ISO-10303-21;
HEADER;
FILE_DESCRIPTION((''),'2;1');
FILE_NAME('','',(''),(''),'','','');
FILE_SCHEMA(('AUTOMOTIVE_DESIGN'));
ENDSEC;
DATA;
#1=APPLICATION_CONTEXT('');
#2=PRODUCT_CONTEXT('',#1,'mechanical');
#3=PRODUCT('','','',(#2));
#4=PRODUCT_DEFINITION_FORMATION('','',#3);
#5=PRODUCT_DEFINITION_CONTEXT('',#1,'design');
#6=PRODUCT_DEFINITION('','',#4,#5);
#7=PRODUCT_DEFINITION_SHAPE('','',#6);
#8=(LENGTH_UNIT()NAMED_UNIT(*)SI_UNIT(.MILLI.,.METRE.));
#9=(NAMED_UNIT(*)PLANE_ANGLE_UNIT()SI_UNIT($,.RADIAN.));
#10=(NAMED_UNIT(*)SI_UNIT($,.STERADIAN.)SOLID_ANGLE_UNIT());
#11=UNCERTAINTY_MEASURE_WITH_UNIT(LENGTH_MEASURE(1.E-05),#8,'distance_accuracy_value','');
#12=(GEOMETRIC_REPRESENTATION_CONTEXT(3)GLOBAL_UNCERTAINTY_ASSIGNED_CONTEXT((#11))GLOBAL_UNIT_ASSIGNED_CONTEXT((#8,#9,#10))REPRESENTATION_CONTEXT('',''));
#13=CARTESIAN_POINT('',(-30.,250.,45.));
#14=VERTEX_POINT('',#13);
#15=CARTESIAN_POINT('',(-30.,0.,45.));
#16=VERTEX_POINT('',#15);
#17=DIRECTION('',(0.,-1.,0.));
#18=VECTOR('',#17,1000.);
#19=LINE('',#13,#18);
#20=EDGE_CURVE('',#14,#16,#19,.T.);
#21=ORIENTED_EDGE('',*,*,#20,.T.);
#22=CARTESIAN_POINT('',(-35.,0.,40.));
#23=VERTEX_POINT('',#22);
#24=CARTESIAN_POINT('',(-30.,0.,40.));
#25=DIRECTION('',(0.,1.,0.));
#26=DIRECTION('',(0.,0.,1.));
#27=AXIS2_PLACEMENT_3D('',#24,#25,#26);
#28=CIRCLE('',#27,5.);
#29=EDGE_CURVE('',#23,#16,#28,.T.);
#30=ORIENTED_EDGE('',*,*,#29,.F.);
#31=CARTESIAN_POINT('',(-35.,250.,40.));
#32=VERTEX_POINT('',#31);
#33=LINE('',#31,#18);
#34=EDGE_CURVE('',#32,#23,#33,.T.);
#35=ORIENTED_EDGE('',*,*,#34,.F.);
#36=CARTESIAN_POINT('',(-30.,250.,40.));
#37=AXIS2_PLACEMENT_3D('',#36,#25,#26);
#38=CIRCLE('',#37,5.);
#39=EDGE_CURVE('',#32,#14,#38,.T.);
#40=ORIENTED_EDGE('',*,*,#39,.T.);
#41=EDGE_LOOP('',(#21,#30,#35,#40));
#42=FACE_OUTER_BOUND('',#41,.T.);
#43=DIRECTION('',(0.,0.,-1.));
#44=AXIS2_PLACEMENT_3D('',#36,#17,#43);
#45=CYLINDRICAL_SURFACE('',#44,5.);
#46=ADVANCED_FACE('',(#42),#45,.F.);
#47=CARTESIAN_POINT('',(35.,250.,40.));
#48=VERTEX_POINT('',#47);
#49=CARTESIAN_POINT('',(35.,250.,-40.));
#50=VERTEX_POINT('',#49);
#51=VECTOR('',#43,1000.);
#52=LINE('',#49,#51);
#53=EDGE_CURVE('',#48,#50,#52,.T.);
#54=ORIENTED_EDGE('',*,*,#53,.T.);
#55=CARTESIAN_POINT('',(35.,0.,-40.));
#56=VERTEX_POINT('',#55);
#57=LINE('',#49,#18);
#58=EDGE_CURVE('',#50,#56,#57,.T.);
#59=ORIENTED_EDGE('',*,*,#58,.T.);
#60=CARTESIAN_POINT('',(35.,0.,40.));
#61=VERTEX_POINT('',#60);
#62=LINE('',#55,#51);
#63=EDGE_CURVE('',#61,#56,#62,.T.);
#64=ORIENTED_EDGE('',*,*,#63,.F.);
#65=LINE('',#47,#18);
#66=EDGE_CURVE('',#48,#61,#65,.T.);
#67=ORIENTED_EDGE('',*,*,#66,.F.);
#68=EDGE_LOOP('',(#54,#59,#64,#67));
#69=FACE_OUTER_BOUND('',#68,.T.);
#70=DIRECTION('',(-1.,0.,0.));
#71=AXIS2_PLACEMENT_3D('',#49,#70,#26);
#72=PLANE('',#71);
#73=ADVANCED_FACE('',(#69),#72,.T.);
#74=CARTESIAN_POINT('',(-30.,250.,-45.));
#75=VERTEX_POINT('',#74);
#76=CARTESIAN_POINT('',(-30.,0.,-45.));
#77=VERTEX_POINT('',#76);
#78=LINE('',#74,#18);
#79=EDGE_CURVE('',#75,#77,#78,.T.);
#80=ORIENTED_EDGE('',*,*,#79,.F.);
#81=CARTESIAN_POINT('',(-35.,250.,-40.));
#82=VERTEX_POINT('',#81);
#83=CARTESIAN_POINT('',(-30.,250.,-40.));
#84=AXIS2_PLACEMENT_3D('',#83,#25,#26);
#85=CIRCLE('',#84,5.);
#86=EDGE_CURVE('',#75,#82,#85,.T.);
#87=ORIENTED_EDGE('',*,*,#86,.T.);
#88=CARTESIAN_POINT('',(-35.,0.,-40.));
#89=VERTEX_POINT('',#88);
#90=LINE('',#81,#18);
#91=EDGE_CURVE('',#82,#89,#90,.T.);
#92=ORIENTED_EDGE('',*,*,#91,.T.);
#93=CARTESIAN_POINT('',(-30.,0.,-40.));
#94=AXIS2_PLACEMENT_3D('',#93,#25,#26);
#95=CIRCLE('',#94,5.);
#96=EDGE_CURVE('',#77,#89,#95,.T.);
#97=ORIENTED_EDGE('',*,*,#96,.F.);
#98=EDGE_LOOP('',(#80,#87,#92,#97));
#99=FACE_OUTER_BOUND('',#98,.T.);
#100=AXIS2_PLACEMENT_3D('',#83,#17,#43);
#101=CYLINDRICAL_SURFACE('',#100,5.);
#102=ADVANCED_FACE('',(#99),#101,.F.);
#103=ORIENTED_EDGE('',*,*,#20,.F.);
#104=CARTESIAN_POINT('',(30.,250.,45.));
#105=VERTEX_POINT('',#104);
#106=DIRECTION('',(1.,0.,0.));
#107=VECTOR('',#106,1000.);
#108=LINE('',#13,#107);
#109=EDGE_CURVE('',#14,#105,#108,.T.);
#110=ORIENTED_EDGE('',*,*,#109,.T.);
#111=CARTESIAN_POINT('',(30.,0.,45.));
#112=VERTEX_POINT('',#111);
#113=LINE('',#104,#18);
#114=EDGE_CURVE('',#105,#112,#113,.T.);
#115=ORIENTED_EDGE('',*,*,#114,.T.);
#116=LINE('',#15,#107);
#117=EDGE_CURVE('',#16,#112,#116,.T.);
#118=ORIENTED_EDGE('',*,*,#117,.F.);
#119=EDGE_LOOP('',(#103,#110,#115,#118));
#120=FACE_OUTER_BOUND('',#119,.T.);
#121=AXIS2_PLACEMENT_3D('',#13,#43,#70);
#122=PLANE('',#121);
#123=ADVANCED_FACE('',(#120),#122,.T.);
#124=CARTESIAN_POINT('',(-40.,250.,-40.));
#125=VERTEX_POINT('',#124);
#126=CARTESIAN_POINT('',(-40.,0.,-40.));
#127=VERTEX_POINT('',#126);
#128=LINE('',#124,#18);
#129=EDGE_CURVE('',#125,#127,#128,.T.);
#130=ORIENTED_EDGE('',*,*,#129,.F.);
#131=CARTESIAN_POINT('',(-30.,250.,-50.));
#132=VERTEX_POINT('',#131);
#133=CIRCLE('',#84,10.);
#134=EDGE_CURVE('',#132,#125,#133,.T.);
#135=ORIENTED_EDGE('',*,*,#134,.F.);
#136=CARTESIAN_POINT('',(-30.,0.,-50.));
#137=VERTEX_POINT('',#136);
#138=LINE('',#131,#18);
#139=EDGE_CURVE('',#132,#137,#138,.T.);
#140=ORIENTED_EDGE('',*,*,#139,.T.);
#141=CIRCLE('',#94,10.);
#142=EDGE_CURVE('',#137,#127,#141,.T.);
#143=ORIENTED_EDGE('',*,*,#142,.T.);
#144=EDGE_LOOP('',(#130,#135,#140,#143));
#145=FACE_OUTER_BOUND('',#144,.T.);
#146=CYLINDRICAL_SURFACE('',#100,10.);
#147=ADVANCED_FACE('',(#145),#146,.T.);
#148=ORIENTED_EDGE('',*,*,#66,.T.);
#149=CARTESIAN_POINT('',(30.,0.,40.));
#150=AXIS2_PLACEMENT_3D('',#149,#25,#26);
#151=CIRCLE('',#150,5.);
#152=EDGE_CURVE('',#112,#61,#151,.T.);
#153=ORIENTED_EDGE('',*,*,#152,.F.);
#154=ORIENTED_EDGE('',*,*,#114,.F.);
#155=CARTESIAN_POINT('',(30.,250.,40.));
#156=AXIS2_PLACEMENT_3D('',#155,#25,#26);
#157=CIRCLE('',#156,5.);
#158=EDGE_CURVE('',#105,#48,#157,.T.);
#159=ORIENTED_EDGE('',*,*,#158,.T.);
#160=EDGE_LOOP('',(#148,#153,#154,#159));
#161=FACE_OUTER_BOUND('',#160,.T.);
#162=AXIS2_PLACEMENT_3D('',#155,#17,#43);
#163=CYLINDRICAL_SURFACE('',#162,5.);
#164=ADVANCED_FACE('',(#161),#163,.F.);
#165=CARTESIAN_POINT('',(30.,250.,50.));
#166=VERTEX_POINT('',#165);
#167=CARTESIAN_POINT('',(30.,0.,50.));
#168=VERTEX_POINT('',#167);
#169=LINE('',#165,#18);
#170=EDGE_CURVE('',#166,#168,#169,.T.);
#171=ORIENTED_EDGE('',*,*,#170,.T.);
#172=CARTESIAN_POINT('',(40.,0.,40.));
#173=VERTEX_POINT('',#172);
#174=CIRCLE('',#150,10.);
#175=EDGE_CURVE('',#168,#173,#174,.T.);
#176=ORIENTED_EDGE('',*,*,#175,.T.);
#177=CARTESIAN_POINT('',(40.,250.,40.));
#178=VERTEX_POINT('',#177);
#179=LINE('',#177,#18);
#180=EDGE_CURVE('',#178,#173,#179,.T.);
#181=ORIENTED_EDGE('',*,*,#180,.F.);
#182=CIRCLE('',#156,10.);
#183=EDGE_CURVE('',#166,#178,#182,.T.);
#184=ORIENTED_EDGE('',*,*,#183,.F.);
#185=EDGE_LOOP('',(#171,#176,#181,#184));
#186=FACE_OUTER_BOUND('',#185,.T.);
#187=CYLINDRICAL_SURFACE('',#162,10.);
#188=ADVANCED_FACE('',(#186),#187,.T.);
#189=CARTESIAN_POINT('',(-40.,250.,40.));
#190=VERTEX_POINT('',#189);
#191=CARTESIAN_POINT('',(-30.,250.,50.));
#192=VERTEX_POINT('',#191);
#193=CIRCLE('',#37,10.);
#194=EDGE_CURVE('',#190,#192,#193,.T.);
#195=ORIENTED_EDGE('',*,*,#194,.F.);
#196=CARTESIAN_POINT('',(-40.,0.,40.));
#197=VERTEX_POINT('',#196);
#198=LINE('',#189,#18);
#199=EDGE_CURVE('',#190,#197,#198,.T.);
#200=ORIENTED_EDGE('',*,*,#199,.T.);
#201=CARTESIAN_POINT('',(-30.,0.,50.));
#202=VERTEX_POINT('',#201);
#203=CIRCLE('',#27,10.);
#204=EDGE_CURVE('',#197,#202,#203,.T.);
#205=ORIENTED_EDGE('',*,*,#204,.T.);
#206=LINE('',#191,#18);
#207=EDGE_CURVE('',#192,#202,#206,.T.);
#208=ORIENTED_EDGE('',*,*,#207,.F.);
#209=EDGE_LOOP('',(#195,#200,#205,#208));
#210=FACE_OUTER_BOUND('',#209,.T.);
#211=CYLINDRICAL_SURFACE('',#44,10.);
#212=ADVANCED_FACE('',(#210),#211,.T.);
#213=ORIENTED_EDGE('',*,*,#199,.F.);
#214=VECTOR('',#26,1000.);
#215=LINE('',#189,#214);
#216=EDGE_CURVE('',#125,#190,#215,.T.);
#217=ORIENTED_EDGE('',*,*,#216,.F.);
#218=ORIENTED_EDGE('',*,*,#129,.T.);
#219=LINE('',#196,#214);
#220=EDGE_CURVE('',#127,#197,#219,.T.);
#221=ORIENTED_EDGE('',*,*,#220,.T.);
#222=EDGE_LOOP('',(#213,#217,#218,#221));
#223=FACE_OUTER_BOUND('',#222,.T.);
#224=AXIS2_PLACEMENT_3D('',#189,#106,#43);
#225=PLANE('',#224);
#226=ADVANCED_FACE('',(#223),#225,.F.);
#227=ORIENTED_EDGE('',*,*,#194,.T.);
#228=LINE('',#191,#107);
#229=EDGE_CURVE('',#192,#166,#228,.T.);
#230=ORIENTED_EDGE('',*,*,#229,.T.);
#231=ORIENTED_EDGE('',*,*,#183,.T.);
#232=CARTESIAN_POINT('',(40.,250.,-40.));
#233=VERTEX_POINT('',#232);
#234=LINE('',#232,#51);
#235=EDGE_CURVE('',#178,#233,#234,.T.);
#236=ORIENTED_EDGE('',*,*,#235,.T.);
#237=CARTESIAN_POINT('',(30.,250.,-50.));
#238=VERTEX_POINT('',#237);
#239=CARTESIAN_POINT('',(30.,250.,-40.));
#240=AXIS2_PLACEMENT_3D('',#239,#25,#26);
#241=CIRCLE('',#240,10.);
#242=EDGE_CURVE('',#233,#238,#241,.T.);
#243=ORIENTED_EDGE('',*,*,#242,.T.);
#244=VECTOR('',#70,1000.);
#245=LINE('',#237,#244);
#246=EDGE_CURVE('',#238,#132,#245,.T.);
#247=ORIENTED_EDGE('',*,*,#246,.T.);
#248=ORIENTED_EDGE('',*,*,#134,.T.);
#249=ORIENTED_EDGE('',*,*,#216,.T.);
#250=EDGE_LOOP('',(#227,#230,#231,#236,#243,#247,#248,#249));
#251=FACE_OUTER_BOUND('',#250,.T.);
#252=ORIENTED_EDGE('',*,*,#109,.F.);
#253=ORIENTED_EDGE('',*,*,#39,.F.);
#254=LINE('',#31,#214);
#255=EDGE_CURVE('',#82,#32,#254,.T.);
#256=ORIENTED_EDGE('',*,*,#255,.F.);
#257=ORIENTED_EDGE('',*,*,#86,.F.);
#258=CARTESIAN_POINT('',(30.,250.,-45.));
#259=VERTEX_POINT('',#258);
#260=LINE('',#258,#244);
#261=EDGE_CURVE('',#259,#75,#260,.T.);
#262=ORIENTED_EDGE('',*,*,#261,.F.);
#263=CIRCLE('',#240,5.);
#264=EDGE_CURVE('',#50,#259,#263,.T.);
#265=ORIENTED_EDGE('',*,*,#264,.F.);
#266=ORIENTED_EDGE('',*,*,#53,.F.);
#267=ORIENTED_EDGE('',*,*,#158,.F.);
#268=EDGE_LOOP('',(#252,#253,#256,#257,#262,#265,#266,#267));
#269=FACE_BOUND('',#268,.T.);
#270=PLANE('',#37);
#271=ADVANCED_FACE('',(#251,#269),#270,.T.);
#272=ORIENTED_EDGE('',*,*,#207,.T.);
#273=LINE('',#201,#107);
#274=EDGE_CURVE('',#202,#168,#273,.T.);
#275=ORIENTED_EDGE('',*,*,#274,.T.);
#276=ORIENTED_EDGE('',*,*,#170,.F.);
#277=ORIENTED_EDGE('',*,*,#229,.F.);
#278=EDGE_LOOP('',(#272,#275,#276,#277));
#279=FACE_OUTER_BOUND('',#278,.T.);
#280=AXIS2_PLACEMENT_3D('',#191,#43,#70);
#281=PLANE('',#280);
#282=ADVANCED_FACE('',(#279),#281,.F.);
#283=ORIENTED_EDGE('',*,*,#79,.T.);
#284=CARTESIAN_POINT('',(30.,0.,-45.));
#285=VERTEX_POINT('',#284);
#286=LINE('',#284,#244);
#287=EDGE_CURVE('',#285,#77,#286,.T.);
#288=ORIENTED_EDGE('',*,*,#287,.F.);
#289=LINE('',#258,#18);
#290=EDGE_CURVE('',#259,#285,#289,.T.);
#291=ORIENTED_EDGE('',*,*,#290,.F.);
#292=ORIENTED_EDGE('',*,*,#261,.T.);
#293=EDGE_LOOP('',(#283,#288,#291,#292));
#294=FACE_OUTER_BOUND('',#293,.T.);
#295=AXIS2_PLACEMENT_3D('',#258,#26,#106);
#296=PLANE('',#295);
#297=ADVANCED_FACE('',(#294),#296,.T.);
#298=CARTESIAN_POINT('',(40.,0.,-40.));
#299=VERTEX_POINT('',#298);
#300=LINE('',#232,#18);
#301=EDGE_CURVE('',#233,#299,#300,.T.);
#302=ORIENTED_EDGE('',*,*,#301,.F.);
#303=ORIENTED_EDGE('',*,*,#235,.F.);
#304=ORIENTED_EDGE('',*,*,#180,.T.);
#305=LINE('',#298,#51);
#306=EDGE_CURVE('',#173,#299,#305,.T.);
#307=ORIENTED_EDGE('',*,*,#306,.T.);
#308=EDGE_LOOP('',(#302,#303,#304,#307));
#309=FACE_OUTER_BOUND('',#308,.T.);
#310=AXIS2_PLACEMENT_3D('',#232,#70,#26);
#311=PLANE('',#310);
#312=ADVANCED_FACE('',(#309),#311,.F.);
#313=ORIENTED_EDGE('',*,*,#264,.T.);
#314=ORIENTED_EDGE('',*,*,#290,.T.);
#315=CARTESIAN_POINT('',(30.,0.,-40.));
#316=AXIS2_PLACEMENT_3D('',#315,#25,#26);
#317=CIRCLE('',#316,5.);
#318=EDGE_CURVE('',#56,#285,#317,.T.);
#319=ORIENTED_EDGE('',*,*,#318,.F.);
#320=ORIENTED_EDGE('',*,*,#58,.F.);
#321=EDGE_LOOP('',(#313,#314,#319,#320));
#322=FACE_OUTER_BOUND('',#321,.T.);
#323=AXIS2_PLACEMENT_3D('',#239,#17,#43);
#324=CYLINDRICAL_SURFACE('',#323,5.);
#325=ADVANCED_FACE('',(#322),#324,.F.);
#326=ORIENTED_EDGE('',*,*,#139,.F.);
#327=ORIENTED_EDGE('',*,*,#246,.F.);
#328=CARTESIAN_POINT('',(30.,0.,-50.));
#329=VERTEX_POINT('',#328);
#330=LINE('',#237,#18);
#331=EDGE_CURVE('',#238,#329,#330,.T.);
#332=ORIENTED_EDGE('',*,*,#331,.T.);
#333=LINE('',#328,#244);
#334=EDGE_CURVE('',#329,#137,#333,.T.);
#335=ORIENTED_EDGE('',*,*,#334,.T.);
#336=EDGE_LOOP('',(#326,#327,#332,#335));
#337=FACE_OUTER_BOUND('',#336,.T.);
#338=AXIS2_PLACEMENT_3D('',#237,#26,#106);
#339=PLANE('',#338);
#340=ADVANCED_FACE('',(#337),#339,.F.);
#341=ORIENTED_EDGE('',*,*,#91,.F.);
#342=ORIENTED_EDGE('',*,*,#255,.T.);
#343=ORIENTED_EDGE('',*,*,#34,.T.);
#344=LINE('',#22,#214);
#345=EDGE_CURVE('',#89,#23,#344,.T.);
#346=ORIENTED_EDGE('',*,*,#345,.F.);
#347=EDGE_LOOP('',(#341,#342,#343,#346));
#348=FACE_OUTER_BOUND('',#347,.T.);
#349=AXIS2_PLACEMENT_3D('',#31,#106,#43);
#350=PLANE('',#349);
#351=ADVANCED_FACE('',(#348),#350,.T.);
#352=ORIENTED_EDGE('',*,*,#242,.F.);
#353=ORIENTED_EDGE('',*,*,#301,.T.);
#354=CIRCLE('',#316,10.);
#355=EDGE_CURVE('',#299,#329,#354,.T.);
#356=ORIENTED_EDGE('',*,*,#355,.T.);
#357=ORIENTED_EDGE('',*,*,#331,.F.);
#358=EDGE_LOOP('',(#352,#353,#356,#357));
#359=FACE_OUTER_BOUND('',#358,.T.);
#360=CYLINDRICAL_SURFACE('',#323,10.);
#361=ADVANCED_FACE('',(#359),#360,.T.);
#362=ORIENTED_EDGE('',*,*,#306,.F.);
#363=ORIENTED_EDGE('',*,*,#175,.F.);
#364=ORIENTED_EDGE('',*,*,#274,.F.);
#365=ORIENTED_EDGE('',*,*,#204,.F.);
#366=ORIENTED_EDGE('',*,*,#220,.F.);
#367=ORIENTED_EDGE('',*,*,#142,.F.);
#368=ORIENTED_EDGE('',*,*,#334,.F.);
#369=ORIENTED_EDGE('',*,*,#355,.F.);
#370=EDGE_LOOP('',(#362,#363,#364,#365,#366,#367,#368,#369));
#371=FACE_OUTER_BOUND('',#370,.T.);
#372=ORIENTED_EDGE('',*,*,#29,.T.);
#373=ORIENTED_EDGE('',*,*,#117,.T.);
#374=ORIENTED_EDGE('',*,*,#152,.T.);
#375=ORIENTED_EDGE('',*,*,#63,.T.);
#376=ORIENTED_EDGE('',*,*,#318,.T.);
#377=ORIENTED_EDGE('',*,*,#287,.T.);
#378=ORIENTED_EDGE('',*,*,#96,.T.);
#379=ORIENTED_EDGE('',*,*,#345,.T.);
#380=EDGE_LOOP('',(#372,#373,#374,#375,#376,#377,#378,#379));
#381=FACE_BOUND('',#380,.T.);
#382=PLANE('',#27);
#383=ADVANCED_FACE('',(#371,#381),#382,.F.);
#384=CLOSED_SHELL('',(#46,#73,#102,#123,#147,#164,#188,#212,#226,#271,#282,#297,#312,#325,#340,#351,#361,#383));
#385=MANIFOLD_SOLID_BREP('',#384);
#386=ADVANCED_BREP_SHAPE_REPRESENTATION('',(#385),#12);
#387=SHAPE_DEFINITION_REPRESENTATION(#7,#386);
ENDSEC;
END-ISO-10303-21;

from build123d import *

# Parameters (mm, degrees)
GB_T_6728_2002_RECTANGULAR_HOLLOW_SECTIO_DEPTH = 250


with BuildPart() as part:
    # Sketch12 → Gb／t 6728—2002 rectangular hollow section 100X80X5(1) (new body)
    with BuildSketch(Plane(origin=(0, 0, 0), x_dir=(-1, 0, 0), z_dir=(0, 1, 0))):
        with BuildLine():
            Line((-30, -50), (30, -50))
            ThreePointArc((30, -50), (37.071067812, -47.071067812), (40, -40))
            Line((40, -40), (40, 40))
            ThreePointArc((40, 40), (37.071067812, 47.071067812), (30, 50))
            Line((30, 50), (-30, 50))
            ThreePointArc((-30, 50), (-37.071067812, 47.071067812), (-40, 40))
            Line((-40, 40), (-40, -40))
            ThreePointArc((-40, -40), (-37.071067812, -47.071067812), (-30, -50))
        make_face()
        with BuildLine():
            Line((-30, -45), (30, -45))
            ThreePointArc((30, -45), (33.535533906, -43.535533906), (35, -40))
            Line((35, -40), (35, 40))
            ThreePointArc((35, 40), (33.535533906, 43.535533906), (30, 45))
            Line((30, 45), (-30, 45))
            ThreePointArc((-30, 45), (-33.535533906, 43.535533906), (-35, 40))
            Line((-35, 40), (-35, -40))
            ThreePointArc((-35, -40), (-33.535533906, -43.535533906), (-30, -45))
        make_face(mode=Mode.SUBTRACT)
    extrude(amount=GB_T_6728_2002_RECTANGULAR_HOLLOW_SECTIO_DEPTH)


solid = part.part
